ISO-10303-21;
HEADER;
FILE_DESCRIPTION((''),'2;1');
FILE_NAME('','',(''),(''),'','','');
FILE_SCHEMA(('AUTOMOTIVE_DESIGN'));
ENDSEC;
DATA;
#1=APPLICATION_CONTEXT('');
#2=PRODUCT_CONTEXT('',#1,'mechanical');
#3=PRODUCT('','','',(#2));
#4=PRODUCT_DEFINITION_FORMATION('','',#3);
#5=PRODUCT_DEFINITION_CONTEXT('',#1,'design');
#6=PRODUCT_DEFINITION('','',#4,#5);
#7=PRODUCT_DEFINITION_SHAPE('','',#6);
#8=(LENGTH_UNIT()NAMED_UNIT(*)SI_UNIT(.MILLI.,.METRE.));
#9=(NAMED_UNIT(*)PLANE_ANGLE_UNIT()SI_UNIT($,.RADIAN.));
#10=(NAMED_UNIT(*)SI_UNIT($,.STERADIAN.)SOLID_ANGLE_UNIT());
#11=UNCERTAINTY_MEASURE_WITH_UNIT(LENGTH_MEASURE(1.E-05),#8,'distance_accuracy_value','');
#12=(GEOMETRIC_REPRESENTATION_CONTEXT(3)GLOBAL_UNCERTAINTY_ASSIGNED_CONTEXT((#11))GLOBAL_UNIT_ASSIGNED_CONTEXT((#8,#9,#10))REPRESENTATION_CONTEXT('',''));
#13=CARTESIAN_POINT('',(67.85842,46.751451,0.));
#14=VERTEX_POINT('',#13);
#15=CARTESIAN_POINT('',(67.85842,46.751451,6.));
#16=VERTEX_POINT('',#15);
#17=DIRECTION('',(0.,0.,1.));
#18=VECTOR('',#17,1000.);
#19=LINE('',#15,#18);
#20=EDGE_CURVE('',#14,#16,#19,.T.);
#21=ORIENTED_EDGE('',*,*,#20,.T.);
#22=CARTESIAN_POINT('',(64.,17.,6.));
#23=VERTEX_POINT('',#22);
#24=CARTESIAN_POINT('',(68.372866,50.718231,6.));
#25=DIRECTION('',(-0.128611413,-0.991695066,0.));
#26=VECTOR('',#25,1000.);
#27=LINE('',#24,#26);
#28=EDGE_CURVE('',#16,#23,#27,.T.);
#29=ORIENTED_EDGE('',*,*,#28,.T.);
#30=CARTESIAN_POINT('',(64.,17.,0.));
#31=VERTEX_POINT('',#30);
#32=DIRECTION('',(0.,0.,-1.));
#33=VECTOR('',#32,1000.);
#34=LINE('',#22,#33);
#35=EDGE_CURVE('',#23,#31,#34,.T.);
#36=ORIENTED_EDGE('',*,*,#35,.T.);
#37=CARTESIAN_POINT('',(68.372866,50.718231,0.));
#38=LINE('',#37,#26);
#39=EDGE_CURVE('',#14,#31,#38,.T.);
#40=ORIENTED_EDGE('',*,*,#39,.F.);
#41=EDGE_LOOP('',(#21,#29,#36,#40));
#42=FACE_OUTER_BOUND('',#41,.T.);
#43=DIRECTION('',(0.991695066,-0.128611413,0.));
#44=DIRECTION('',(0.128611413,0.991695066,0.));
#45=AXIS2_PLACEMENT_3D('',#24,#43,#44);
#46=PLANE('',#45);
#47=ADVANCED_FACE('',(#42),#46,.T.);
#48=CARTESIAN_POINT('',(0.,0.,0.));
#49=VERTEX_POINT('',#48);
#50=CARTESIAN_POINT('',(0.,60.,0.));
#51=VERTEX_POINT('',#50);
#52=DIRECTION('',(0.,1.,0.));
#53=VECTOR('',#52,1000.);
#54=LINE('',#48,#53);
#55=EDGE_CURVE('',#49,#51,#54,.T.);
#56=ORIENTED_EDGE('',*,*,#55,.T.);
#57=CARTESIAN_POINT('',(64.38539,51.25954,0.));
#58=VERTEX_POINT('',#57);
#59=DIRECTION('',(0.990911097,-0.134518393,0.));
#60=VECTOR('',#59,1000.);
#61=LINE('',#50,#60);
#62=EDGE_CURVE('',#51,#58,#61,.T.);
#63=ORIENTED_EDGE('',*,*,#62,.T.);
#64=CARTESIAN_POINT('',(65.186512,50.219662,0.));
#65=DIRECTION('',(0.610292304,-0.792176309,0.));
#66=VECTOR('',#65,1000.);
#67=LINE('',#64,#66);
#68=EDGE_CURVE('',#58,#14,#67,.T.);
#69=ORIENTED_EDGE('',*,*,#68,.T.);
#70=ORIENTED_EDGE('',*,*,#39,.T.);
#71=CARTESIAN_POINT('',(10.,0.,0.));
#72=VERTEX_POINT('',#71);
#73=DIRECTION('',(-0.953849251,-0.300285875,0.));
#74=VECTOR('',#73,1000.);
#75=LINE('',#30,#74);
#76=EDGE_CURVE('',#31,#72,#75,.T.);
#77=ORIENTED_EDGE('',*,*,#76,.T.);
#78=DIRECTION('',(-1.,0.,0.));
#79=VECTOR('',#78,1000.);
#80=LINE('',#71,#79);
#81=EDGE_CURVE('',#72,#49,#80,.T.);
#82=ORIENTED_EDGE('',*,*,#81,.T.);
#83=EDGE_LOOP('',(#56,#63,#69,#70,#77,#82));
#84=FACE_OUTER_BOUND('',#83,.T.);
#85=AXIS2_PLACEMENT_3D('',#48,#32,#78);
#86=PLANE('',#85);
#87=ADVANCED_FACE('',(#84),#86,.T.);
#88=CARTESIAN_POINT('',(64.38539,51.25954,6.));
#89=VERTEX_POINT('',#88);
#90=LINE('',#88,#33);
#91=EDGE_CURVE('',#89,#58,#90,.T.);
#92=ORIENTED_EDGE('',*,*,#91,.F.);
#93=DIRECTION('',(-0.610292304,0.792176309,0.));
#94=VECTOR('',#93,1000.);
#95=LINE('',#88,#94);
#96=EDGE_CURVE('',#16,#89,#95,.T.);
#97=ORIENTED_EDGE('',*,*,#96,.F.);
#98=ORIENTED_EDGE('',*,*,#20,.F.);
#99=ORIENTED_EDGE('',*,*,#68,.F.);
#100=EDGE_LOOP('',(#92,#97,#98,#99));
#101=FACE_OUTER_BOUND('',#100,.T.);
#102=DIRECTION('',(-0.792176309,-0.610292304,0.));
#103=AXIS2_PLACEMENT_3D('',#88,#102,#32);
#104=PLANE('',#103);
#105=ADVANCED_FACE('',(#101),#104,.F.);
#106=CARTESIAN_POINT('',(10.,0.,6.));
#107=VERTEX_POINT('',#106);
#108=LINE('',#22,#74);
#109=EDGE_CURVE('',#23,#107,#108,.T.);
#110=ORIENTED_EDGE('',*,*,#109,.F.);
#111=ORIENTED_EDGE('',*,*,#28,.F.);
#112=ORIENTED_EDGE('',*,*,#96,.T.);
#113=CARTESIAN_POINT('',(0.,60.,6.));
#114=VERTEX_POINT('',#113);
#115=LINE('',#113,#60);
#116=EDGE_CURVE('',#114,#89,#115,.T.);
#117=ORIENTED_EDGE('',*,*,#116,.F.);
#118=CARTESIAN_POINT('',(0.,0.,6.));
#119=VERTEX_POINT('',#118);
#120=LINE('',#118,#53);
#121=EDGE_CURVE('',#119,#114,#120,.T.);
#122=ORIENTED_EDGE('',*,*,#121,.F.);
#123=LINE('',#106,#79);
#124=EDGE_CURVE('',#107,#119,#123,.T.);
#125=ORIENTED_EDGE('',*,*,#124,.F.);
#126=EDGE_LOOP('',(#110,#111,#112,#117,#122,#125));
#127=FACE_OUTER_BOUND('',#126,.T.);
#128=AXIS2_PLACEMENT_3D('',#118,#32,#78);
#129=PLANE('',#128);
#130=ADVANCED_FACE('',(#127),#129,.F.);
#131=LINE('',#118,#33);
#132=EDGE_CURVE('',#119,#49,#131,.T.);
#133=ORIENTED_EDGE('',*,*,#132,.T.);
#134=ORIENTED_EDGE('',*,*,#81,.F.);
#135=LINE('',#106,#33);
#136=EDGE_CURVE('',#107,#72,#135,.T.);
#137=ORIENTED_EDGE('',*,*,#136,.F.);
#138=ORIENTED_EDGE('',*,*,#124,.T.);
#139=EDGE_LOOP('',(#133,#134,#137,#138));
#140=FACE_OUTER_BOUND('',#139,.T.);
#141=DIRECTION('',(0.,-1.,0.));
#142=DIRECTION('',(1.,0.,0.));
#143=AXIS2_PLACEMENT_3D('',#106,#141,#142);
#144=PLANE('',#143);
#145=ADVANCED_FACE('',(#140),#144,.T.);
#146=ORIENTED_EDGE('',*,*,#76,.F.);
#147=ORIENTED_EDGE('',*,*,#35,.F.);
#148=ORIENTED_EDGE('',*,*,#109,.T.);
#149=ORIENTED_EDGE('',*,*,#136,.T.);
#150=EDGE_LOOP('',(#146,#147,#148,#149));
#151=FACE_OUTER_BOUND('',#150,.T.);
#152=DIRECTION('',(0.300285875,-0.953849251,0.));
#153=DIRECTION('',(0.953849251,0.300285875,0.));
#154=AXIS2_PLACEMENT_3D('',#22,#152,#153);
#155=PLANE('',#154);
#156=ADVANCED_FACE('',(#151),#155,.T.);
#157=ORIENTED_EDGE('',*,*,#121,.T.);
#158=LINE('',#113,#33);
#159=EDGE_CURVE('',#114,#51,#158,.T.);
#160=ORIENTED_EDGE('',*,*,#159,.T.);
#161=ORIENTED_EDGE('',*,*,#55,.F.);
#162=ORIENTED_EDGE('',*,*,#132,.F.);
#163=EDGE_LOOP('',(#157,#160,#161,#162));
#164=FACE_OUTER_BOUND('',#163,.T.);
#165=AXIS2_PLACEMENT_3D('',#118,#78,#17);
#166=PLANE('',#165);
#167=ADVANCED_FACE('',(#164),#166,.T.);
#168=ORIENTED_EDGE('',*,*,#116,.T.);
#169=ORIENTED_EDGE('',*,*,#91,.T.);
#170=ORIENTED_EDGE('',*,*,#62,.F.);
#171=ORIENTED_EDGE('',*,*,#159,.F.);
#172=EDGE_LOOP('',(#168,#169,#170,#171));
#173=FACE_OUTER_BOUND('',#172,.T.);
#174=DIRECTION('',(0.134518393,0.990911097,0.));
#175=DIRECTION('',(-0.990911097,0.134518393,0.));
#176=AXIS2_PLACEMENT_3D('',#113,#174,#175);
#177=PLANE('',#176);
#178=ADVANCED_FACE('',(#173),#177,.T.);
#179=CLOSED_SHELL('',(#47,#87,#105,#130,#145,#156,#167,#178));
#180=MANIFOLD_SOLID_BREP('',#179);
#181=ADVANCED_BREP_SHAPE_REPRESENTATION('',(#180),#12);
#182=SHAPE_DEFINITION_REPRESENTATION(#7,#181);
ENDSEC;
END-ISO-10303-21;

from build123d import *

# Parameters (mm, degrees)
BOSS_EXTRUDE1_DEPTH = 6
CHAMFER1_SIZE       = 4
CHAMFER1_SIZE2      = 4.024049749


with BuildPart() as part:
    # Sketch1 → Boss-Extrude1 (new body)
    with BuildSketch(Plane.XY):
        Polygon((0, 0), (0, 60), (68.372865684, 50.718230869), (64, 17), (10, 0), align=None)
    extrude(amount=BOSS_EXTRUDE1_DEPTH)

    # Chamfer1
    chamfer1_edges = [part.edges().sort_by_distance(p)[0] for p in [
        (68.372865684, 50.718230869, 3),
    ]]
    chamfer1_side = [part.faces().sort_by_distance(p)[0] for p in [
        (66.186432842, 33.859115434, 3),
    ]]
    chamfer(chamfer1_edges, length=CHAMFER1_SIZE, length2=CHAMFER1_SIZE2, reference=chamfer1_side[0])


solid = part.part
